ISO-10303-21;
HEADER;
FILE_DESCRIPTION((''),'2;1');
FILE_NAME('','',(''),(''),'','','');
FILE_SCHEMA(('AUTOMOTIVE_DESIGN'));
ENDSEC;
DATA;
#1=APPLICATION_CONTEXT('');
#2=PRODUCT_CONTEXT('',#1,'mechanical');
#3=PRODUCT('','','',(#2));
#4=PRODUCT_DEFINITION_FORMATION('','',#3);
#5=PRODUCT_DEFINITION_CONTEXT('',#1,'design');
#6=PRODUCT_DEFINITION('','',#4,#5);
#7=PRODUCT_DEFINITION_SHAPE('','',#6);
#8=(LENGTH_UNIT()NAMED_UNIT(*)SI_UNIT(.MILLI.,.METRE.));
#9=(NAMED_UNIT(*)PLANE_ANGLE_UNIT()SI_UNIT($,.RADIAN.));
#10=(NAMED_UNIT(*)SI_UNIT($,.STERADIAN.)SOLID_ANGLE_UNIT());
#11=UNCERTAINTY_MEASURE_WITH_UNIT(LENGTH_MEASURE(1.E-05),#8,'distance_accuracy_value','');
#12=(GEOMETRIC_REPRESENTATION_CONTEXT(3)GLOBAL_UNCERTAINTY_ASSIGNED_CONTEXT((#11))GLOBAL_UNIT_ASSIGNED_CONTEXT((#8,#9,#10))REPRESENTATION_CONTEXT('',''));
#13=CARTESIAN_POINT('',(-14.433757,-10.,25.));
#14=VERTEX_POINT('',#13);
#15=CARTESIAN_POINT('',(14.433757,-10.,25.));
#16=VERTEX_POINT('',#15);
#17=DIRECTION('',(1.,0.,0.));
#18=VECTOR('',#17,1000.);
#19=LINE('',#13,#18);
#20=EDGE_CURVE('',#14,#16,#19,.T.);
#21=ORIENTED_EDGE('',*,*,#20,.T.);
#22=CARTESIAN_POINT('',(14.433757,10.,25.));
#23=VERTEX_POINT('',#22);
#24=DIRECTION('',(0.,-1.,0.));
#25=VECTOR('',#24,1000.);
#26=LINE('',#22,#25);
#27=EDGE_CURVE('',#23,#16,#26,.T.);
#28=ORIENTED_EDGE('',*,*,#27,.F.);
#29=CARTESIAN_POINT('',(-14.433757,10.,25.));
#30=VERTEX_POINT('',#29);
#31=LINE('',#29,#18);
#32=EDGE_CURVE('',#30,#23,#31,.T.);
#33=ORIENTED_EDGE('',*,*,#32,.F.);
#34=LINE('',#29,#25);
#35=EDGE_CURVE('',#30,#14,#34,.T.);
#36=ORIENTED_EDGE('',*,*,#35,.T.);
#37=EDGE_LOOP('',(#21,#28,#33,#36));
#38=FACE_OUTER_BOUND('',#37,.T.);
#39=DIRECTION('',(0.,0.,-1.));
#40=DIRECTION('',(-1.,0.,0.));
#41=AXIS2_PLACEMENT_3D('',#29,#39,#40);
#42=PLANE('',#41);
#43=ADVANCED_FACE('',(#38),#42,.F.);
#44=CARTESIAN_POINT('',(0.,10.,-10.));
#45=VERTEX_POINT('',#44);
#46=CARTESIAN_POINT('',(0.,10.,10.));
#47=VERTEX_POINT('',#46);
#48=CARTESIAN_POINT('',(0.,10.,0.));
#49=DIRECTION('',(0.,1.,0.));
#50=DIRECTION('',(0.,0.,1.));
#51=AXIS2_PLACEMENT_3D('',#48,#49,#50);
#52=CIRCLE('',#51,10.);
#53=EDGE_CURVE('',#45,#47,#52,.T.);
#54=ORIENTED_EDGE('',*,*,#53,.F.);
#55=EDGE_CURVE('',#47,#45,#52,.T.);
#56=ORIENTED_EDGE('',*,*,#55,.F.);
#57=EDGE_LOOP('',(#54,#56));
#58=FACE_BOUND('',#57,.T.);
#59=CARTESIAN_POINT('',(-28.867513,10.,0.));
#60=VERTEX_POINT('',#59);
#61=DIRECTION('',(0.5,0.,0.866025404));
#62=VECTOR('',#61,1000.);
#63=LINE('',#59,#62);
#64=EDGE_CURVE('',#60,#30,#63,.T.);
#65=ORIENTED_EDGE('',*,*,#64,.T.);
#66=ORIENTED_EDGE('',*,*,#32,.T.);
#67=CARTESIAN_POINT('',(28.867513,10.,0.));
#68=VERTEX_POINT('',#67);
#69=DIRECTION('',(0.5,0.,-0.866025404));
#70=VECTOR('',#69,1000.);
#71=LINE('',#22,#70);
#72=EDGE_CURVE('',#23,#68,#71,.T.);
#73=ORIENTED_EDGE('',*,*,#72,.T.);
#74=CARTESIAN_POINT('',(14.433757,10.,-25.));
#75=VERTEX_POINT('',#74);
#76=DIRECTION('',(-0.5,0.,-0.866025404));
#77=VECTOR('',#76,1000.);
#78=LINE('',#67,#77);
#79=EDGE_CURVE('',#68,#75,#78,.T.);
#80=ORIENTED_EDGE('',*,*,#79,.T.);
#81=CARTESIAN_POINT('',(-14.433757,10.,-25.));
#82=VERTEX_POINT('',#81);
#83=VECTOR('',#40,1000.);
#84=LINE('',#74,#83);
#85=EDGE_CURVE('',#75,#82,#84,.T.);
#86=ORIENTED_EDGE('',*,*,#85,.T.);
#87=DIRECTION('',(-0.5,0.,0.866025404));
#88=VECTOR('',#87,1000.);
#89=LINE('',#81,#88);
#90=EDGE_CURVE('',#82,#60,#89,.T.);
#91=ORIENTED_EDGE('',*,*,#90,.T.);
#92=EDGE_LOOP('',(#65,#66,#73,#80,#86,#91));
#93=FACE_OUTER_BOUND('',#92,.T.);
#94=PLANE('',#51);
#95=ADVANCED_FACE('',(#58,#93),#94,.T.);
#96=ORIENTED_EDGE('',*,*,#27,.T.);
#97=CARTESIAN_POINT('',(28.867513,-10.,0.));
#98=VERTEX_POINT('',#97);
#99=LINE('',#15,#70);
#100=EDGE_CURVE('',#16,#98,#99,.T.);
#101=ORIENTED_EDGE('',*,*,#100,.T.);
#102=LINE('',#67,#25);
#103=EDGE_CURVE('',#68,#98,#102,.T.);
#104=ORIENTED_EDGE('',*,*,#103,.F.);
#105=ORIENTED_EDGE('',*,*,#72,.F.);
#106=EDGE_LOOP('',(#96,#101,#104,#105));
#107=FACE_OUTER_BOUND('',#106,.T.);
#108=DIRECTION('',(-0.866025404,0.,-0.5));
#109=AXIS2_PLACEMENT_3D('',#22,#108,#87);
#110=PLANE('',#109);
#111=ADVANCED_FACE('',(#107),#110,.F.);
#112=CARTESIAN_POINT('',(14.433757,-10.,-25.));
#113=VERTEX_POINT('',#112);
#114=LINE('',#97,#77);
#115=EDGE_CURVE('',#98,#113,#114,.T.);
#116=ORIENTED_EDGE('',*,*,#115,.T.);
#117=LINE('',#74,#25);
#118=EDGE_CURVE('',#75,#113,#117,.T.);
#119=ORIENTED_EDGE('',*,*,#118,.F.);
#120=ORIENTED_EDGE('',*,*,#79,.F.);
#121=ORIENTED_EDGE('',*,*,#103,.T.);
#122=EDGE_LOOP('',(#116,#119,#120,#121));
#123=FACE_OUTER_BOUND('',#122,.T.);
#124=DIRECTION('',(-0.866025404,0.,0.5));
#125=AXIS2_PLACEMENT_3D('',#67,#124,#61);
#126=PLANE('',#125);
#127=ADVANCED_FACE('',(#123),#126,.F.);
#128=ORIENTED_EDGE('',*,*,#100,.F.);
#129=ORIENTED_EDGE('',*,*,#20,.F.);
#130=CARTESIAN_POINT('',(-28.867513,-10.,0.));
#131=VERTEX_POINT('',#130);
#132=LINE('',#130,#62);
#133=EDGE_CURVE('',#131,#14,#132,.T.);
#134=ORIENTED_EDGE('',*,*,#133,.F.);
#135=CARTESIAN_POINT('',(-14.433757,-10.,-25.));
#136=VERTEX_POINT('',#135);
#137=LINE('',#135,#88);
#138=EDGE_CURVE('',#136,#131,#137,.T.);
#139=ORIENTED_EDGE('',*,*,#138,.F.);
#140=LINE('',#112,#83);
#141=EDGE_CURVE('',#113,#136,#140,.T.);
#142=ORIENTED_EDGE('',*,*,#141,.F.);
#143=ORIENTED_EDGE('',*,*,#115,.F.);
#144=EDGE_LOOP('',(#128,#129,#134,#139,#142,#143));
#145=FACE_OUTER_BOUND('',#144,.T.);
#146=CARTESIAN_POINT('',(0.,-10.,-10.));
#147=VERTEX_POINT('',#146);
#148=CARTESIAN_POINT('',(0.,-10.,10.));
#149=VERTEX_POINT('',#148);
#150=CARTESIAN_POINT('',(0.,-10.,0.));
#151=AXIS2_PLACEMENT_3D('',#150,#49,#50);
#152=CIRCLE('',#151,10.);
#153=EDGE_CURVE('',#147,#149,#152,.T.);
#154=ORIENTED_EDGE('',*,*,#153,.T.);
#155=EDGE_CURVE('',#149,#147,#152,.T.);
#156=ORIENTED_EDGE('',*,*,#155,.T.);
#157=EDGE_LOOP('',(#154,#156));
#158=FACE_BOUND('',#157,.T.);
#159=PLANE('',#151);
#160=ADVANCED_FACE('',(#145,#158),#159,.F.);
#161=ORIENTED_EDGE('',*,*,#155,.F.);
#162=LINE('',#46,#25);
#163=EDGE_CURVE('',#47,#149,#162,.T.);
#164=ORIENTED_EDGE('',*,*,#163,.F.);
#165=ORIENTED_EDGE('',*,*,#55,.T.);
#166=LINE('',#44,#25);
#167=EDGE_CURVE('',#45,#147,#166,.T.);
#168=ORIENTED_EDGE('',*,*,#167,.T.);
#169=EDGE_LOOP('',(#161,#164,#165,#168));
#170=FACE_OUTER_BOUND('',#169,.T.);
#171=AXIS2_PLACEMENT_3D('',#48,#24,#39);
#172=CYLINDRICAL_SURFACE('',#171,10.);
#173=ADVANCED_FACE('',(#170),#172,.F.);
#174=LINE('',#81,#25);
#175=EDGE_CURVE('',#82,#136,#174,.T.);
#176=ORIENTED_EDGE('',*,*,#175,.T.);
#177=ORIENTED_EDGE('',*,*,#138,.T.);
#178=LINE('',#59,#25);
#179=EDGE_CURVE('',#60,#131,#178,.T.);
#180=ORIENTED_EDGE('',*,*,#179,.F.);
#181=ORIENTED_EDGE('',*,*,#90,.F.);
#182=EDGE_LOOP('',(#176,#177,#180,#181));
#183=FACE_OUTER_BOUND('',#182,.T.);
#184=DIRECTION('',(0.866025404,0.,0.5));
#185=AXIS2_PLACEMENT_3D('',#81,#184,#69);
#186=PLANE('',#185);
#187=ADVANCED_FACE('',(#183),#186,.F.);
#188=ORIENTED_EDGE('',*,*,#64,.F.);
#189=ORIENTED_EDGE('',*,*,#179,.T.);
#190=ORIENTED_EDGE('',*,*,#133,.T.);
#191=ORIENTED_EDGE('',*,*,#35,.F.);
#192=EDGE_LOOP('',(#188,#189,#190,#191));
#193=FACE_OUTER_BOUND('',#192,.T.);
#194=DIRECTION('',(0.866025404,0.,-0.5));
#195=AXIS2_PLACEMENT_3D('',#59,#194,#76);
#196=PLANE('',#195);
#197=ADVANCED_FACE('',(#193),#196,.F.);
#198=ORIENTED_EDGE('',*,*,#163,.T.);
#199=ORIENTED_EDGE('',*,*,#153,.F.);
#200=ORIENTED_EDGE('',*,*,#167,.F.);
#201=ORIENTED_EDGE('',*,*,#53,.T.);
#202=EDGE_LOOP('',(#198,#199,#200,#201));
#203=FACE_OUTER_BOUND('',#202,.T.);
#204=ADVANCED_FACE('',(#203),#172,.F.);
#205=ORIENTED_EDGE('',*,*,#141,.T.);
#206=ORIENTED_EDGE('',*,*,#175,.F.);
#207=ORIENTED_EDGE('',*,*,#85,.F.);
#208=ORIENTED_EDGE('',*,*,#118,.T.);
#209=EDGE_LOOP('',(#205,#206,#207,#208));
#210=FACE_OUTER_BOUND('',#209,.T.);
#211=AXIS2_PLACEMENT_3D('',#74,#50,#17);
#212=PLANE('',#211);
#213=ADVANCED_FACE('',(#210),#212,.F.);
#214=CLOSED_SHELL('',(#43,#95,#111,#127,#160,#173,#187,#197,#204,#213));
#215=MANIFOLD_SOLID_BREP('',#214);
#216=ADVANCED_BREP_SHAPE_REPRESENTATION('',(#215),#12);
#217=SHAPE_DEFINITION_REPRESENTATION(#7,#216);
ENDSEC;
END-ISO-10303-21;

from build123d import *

# Parameters (mm, degrees)
HEX_NUT_PROFILE_R  = 10
HEX_NUT_BODY_DEPTH = 10


with BuildPart() as part:
    # Hex Nut Profile → Hex Nut Body (new, symmetric)
    with BuildSketch(Plane(origin=(0, 0, 0), x_dir=(1, 0, 0), z_dir=(0, 1, 0))):
        Polygon((28.867513459, 0), (14.43375673, 25), (-14.43375673, 25), (-28.867513459, 0), (-14.43375673, -25), (14.43375673, -25), align=None)
        with Locations(Location((0, 0, 0), (0, 0, 270))):
            Circle(HEX_NUT_PROFILE_R, mode=Mode.SUBTRACT)
    extrude(amount=HEX_NUT_BODY_DEPTH, both=True)


solid = part.part
